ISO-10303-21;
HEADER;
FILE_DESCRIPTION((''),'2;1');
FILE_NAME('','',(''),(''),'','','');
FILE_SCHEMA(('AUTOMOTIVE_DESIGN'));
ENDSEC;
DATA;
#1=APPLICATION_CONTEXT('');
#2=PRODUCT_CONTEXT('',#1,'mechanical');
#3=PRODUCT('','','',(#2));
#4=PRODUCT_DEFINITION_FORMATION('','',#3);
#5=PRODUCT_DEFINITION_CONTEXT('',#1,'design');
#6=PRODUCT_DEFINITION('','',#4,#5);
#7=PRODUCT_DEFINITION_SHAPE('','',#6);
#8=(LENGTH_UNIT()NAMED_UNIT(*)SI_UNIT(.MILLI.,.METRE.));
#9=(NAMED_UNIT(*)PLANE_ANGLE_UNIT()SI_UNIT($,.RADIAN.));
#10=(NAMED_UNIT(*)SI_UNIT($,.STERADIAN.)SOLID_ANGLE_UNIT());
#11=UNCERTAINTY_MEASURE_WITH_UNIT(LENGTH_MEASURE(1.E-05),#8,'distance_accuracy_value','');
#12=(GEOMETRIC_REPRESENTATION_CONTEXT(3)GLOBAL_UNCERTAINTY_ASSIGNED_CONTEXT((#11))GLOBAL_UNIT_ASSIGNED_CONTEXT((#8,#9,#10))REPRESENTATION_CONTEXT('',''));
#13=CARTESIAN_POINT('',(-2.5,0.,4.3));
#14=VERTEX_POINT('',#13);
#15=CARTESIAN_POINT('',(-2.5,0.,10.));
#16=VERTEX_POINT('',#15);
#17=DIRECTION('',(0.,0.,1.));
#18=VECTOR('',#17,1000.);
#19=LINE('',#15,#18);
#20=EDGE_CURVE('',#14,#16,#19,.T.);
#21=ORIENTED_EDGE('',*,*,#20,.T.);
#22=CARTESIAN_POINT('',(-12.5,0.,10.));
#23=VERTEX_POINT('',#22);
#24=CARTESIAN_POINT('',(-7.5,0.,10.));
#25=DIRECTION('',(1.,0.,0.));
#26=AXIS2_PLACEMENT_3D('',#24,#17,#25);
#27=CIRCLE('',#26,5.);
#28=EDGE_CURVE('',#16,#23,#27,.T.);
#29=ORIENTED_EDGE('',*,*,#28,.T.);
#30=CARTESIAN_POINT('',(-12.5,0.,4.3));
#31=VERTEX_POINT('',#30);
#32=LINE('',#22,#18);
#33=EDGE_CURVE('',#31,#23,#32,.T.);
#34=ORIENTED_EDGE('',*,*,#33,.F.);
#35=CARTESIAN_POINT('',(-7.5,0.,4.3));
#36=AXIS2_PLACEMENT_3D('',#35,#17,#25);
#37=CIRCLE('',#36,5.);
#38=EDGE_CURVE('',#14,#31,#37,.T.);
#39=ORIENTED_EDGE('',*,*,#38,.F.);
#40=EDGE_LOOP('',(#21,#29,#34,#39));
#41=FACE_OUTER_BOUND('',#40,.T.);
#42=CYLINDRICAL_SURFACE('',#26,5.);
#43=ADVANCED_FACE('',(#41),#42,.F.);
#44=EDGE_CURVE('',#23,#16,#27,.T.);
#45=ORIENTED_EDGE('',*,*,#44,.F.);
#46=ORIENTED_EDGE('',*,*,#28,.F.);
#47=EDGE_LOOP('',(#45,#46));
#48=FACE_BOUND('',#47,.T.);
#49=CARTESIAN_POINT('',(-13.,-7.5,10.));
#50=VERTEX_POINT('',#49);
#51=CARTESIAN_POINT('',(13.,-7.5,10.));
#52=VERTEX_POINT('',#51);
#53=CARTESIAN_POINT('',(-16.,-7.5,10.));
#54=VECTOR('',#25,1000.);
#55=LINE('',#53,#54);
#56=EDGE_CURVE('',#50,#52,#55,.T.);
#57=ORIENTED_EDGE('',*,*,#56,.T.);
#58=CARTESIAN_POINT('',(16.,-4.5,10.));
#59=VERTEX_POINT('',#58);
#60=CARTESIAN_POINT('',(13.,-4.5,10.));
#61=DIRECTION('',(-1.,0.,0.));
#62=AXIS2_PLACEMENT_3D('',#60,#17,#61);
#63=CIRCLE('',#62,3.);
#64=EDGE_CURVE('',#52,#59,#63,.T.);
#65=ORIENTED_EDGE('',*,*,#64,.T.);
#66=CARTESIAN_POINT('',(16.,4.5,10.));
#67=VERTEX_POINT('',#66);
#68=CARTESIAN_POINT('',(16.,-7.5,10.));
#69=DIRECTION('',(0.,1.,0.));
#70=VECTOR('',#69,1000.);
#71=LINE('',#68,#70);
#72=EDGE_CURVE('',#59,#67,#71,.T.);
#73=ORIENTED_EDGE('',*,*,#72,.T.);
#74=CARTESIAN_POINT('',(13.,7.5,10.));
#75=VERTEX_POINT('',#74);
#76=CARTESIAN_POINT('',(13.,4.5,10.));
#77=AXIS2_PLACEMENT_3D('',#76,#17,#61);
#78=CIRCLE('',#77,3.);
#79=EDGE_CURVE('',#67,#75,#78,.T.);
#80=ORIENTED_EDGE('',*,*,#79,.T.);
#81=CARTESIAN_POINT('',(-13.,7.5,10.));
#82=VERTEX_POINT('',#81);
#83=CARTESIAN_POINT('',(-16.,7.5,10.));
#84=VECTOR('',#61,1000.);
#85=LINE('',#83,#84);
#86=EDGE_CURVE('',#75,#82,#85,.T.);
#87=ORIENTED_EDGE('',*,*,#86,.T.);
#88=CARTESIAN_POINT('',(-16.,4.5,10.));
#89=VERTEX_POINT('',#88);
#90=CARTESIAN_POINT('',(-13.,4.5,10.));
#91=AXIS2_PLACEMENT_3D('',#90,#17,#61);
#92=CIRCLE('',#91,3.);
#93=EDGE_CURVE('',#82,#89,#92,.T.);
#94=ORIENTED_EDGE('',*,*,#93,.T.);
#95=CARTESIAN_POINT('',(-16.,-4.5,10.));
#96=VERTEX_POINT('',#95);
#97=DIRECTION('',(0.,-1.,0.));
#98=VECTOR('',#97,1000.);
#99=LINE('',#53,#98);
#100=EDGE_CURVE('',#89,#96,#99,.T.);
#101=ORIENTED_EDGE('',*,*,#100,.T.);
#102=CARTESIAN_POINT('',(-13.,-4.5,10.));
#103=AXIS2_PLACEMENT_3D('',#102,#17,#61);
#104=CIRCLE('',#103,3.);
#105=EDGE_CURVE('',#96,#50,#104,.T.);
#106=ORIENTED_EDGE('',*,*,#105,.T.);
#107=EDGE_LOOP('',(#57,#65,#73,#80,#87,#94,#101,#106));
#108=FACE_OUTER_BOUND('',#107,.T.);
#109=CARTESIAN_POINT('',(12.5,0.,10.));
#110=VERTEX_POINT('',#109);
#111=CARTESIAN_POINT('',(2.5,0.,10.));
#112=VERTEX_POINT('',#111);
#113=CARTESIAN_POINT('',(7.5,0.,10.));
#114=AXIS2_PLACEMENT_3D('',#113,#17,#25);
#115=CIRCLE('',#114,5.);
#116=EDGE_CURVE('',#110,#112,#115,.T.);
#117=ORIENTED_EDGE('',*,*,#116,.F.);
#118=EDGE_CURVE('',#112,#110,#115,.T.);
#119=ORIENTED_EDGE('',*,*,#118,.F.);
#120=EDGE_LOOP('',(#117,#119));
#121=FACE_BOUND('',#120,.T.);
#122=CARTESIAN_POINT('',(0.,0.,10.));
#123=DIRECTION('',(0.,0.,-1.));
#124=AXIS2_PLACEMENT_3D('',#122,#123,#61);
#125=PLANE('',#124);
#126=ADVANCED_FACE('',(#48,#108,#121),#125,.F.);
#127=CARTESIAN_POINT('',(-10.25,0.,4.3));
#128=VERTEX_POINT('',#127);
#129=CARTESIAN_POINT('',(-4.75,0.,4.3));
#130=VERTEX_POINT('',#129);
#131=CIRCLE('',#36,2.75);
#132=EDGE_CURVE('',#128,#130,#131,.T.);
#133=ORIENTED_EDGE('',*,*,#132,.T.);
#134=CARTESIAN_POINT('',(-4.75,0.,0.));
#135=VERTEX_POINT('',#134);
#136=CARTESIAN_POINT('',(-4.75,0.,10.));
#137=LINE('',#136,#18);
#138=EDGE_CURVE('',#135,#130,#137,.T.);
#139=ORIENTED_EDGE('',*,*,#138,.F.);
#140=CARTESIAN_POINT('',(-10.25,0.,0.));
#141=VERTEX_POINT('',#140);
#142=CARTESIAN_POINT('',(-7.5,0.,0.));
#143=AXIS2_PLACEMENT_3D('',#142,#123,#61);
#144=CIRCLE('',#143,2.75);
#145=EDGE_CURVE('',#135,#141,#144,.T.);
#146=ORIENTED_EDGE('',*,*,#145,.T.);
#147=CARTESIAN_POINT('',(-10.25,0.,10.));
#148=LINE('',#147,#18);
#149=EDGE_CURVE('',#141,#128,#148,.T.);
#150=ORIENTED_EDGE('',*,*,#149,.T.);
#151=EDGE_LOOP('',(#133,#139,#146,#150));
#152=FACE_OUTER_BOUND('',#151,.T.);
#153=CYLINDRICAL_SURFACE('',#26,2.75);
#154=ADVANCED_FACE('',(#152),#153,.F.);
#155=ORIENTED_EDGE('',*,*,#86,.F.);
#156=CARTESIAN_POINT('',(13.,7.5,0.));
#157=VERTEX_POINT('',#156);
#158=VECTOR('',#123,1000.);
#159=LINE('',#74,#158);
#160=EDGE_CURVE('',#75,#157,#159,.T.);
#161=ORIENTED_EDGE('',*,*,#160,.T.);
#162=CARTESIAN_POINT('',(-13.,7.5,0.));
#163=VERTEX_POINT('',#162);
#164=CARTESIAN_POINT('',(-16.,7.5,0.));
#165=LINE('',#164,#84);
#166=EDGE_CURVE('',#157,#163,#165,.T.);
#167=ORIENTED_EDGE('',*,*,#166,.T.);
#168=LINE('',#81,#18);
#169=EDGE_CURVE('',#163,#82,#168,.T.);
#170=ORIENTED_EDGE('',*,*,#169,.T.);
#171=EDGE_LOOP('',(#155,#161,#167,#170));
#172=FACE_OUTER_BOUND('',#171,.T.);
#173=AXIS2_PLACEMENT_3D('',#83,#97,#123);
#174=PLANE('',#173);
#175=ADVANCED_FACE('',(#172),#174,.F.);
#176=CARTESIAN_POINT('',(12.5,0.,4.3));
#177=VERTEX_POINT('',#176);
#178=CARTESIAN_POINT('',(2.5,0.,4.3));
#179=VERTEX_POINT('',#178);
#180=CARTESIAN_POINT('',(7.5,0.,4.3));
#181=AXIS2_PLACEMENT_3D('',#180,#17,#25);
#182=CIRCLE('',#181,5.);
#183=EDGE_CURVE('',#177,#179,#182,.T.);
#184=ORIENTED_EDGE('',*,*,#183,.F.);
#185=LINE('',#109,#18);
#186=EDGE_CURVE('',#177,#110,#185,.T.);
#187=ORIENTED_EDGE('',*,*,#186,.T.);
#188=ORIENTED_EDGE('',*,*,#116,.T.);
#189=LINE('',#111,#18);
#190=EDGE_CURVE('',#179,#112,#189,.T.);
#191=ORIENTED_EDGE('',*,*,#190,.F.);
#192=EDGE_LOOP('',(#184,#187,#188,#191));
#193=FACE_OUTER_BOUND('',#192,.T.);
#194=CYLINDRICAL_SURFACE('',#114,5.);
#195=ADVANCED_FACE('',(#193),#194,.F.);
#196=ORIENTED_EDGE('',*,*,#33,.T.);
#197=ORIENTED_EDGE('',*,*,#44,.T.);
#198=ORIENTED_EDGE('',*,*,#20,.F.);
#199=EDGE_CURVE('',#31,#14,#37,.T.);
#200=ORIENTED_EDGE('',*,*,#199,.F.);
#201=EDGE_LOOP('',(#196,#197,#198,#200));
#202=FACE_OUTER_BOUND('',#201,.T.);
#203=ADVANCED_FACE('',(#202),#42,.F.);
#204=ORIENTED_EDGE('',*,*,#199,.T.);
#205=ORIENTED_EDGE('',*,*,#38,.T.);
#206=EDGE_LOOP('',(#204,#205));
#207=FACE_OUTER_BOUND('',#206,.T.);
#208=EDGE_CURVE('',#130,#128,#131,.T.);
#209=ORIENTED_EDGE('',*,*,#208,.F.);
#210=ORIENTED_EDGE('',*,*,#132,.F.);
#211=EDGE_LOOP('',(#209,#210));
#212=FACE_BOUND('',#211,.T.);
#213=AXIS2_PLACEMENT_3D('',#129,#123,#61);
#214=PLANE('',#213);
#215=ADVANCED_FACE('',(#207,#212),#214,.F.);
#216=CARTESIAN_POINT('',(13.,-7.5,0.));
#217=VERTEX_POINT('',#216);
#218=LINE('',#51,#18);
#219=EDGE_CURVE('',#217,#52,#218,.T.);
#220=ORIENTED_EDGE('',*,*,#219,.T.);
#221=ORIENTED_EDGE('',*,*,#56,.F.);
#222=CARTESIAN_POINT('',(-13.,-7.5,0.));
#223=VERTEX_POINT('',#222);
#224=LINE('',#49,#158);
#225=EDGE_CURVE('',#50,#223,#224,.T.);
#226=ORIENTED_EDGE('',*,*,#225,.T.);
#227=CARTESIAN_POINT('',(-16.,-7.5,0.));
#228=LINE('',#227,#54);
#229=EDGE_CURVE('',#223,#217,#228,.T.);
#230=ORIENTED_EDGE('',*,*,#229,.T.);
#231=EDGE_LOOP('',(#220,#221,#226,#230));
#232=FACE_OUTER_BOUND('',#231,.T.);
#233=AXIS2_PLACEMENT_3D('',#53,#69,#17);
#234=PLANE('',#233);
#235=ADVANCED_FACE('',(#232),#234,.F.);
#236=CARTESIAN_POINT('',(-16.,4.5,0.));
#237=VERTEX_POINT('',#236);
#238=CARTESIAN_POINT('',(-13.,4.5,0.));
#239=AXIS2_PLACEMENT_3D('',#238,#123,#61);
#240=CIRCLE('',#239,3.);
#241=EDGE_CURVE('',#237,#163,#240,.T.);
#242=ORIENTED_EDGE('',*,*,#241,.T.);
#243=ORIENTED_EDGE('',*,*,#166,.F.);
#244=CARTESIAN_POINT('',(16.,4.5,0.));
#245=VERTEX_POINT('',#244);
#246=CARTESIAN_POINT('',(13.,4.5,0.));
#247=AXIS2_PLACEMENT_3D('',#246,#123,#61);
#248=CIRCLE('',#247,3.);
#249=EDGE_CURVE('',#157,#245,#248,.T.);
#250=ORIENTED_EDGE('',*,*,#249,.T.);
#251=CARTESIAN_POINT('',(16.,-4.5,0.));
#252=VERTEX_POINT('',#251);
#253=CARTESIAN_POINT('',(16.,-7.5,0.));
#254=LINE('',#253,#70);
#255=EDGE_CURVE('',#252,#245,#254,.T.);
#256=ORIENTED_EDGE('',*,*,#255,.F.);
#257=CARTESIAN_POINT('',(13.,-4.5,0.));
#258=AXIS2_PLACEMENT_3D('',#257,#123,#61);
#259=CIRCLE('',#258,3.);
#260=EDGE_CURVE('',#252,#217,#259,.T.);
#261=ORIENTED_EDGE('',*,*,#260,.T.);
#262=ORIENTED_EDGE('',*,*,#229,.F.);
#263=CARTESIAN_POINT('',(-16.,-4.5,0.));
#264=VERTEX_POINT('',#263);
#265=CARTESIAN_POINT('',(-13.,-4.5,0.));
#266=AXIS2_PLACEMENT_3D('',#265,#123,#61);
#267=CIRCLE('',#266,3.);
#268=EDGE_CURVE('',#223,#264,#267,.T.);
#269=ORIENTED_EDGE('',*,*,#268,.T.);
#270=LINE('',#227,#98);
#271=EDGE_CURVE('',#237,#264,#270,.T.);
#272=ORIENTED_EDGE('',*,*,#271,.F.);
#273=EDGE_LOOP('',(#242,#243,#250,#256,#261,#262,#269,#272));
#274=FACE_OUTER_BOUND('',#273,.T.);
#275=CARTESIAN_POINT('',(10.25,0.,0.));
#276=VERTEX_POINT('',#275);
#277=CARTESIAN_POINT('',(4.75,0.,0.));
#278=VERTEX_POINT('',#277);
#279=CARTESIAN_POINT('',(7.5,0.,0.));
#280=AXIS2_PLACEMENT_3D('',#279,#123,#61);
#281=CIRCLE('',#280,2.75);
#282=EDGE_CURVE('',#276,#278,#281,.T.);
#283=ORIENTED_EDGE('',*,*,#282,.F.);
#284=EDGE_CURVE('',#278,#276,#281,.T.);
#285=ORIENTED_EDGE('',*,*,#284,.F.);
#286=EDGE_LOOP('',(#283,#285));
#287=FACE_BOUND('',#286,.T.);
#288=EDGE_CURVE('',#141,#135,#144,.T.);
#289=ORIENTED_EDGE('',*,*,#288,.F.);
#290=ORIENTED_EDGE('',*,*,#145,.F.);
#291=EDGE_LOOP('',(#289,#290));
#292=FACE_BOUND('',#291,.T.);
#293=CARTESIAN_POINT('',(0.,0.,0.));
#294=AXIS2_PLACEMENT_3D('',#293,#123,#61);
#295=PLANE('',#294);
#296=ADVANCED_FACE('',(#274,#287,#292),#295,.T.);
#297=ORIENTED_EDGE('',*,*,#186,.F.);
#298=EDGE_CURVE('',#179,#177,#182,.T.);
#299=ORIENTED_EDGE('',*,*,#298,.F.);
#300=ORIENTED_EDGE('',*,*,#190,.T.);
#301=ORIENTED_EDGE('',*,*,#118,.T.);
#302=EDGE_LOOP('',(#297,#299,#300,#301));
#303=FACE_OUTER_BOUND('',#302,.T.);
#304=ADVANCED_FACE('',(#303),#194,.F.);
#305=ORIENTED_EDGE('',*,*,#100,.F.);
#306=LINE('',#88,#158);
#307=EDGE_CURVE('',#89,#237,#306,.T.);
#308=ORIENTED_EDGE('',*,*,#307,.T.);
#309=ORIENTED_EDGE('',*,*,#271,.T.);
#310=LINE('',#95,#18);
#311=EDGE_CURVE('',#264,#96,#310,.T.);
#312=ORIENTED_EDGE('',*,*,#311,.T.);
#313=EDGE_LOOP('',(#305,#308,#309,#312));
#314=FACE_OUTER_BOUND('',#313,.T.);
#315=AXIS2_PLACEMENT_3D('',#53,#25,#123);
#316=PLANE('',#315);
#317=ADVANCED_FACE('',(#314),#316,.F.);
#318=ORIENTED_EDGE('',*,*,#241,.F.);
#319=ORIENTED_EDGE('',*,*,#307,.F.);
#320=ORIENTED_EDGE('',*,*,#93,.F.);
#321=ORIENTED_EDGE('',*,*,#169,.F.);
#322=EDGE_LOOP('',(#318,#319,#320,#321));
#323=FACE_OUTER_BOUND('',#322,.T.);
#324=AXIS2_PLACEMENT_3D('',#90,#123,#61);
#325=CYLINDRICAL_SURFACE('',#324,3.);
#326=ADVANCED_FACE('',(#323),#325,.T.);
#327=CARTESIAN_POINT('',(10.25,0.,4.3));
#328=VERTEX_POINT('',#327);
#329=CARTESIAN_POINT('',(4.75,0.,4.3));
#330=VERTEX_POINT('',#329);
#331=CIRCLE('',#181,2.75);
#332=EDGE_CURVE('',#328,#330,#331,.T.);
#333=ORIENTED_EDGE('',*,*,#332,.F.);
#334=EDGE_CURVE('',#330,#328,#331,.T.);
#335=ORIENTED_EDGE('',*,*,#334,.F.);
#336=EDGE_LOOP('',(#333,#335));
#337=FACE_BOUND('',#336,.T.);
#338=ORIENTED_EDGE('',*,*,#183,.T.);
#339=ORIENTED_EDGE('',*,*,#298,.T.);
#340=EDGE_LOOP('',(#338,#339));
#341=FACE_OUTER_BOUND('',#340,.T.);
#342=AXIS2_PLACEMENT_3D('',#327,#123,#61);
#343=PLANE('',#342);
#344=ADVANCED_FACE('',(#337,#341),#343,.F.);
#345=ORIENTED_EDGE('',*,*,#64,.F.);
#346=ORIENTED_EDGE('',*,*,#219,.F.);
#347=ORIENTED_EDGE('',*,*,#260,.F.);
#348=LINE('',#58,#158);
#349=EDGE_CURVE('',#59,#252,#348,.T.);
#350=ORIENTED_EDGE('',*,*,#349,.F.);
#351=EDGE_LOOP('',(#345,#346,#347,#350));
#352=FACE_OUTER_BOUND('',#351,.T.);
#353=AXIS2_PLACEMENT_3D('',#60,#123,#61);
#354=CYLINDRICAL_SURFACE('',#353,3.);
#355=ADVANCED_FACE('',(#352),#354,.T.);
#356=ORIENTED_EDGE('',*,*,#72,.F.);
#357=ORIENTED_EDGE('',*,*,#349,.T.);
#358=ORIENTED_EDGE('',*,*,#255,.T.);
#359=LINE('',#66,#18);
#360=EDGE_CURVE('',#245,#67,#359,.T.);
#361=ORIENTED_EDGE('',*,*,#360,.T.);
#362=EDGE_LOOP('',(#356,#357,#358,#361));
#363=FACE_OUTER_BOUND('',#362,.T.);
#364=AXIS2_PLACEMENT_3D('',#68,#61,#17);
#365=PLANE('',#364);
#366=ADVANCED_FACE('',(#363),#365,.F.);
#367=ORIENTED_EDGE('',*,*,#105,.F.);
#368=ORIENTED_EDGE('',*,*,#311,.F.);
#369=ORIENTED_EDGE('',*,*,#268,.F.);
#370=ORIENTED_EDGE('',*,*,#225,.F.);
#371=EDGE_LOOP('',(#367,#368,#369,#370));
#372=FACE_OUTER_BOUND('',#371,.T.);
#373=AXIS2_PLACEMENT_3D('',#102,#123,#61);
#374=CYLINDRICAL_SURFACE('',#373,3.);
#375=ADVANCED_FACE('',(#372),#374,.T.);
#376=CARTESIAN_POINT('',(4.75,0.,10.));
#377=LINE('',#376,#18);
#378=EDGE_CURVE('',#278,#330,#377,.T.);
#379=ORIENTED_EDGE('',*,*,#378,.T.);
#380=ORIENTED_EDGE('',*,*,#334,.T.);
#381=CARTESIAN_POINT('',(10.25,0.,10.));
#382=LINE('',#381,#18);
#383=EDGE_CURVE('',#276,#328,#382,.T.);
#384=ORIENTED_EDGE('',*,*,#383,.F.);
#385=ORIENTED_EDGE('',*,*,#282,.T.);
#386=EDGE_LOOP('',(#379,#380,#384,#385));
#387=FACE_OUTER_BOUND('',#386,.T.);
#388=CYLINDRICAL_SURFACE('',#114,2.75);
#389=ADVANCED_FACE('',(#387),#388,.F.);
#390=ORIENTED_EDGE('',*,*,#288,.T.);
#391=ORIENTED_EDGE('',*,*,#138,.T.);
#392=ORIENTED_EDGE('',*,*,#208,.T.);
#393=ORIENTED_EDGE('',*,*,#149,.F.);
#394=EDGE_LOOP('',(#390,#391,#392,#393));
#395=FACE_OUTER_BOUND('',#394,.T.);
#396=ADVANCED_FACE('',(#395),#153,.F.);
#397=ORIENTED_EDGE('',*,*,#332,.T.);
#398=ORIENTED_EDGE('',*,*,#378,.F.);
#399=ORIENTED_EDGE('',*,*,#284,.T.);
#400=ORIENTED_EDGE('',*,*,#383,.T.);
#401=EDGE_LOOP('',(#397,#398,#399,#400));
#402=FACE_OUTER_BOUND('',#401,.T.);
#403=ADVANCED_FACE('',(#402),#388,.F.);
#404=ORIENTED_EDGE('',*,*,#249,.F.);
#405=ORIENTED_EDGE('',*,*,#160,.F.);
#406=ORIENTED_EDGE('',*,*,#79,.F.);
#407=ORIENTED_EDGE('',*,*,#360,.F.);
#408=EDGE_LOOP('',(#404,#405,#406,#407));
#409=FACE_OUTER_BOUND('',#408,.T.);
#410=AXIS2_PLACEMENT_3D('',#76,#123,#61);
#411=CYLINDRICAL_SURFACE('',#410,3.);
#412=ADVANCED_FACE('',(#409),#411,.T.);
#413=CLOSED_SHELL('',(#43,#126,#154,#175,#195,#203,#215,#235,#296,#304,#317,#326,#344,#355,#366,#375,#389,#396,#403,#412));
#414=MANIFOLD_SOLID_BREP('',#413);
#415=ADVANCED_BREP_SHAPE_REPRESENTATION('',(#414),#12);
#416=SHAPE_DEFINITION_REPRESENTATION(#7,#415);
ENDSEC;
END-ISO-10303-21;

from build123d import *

# Parameters (mm, degrees)
SKETCH1_W                                            = 32
SKETCH1_H                                            = 15
BOSS_EXTRUDE1_DEPTH                                  = 10
CBORE_FOR_M5_HEXAGON_SOCKET_HEAD_CAP_SCR_D           = 5.5
CBORE_FOR_M5_HEXAGON_SOCKET_HEAD_CAP_SCR_DEPTH       = 12.4
CBORE_FOR_M5_HEXAGON_SOCKET_HEAD_CAP_SCR_CBORE_D     = 10
CBORE_FOR_M5_HEXAGON_SOCKET_HEAD_CAP_SCR_CBORE_DEPTH = 5.7
CBORE_FOR_M5_HEXAGON_SOCKET_HEAD_CAP_SCR_TIP         = 1.652366702
FILLET1_R                                            = 3


with BuildPart() as part:
    # Sketch1 → Boss-Extrude1 (new body)
    with BuildSketch(Plane.XY):
        Rectangle(SKETCH1_W, SKETCH1_H)
    extrude(amount=BOSS_EXTRUDE1_DEPTH)

    # CBORE for M5 Hexagon socket head cap screws1
    with Locations(Plane.XY.offset(10)):
        with Locations((7.5, 0), (-7.5, 0)):
            CounterBoreHole(CBORE_FOR_M5_HEXAGON_SOCKET_HEAD_CAP_SCR_D / 2, CBORE_FOR_M5_HEXAGON_SOCKET_HEAD_CAP_SCR_CBORE_D / 2, CBORE_FOR_M5_HEXAGON_SOCKET_HEAD_CAP_SCR_CBORE_DEPTH, depth=CBORE_FOR_M5_HEXAGON_SOCKET_HEAD_CAP_SCR_DEPTH)
            with Locations((0, 0, -(CBORE_FOR_M5_HEXAGON_SOCKET_HEAD_CAP_SCR_DEPTH + CBORE_FOR_M5_HEXAGON_SOCKET_HEAD_CAP_SCR_TIP / 2))):  # 118° drill point
                Cone(0, CBORE_FOR_M5_HEXAGON_SOCKET_HEAD_CAP_SCR_D / 2, CBORE_FOR_M5_HEXAGON_SOCKET_HEAD_CAP_SCR_TIP, mode=Mode.SUBTRACT)

    # Fillet1
    fillet1_edges = [part.edges().sort_by_distance(p)[0] for p in [
        (16, -7.5, 5),
        (-16, -7.5, 5),
        (-16, 7.5, 5),
        (16, 7.5, 5),
    ]]
    fillet(fillet1_edges, radius=FILLET1_R)


solid = part.part
